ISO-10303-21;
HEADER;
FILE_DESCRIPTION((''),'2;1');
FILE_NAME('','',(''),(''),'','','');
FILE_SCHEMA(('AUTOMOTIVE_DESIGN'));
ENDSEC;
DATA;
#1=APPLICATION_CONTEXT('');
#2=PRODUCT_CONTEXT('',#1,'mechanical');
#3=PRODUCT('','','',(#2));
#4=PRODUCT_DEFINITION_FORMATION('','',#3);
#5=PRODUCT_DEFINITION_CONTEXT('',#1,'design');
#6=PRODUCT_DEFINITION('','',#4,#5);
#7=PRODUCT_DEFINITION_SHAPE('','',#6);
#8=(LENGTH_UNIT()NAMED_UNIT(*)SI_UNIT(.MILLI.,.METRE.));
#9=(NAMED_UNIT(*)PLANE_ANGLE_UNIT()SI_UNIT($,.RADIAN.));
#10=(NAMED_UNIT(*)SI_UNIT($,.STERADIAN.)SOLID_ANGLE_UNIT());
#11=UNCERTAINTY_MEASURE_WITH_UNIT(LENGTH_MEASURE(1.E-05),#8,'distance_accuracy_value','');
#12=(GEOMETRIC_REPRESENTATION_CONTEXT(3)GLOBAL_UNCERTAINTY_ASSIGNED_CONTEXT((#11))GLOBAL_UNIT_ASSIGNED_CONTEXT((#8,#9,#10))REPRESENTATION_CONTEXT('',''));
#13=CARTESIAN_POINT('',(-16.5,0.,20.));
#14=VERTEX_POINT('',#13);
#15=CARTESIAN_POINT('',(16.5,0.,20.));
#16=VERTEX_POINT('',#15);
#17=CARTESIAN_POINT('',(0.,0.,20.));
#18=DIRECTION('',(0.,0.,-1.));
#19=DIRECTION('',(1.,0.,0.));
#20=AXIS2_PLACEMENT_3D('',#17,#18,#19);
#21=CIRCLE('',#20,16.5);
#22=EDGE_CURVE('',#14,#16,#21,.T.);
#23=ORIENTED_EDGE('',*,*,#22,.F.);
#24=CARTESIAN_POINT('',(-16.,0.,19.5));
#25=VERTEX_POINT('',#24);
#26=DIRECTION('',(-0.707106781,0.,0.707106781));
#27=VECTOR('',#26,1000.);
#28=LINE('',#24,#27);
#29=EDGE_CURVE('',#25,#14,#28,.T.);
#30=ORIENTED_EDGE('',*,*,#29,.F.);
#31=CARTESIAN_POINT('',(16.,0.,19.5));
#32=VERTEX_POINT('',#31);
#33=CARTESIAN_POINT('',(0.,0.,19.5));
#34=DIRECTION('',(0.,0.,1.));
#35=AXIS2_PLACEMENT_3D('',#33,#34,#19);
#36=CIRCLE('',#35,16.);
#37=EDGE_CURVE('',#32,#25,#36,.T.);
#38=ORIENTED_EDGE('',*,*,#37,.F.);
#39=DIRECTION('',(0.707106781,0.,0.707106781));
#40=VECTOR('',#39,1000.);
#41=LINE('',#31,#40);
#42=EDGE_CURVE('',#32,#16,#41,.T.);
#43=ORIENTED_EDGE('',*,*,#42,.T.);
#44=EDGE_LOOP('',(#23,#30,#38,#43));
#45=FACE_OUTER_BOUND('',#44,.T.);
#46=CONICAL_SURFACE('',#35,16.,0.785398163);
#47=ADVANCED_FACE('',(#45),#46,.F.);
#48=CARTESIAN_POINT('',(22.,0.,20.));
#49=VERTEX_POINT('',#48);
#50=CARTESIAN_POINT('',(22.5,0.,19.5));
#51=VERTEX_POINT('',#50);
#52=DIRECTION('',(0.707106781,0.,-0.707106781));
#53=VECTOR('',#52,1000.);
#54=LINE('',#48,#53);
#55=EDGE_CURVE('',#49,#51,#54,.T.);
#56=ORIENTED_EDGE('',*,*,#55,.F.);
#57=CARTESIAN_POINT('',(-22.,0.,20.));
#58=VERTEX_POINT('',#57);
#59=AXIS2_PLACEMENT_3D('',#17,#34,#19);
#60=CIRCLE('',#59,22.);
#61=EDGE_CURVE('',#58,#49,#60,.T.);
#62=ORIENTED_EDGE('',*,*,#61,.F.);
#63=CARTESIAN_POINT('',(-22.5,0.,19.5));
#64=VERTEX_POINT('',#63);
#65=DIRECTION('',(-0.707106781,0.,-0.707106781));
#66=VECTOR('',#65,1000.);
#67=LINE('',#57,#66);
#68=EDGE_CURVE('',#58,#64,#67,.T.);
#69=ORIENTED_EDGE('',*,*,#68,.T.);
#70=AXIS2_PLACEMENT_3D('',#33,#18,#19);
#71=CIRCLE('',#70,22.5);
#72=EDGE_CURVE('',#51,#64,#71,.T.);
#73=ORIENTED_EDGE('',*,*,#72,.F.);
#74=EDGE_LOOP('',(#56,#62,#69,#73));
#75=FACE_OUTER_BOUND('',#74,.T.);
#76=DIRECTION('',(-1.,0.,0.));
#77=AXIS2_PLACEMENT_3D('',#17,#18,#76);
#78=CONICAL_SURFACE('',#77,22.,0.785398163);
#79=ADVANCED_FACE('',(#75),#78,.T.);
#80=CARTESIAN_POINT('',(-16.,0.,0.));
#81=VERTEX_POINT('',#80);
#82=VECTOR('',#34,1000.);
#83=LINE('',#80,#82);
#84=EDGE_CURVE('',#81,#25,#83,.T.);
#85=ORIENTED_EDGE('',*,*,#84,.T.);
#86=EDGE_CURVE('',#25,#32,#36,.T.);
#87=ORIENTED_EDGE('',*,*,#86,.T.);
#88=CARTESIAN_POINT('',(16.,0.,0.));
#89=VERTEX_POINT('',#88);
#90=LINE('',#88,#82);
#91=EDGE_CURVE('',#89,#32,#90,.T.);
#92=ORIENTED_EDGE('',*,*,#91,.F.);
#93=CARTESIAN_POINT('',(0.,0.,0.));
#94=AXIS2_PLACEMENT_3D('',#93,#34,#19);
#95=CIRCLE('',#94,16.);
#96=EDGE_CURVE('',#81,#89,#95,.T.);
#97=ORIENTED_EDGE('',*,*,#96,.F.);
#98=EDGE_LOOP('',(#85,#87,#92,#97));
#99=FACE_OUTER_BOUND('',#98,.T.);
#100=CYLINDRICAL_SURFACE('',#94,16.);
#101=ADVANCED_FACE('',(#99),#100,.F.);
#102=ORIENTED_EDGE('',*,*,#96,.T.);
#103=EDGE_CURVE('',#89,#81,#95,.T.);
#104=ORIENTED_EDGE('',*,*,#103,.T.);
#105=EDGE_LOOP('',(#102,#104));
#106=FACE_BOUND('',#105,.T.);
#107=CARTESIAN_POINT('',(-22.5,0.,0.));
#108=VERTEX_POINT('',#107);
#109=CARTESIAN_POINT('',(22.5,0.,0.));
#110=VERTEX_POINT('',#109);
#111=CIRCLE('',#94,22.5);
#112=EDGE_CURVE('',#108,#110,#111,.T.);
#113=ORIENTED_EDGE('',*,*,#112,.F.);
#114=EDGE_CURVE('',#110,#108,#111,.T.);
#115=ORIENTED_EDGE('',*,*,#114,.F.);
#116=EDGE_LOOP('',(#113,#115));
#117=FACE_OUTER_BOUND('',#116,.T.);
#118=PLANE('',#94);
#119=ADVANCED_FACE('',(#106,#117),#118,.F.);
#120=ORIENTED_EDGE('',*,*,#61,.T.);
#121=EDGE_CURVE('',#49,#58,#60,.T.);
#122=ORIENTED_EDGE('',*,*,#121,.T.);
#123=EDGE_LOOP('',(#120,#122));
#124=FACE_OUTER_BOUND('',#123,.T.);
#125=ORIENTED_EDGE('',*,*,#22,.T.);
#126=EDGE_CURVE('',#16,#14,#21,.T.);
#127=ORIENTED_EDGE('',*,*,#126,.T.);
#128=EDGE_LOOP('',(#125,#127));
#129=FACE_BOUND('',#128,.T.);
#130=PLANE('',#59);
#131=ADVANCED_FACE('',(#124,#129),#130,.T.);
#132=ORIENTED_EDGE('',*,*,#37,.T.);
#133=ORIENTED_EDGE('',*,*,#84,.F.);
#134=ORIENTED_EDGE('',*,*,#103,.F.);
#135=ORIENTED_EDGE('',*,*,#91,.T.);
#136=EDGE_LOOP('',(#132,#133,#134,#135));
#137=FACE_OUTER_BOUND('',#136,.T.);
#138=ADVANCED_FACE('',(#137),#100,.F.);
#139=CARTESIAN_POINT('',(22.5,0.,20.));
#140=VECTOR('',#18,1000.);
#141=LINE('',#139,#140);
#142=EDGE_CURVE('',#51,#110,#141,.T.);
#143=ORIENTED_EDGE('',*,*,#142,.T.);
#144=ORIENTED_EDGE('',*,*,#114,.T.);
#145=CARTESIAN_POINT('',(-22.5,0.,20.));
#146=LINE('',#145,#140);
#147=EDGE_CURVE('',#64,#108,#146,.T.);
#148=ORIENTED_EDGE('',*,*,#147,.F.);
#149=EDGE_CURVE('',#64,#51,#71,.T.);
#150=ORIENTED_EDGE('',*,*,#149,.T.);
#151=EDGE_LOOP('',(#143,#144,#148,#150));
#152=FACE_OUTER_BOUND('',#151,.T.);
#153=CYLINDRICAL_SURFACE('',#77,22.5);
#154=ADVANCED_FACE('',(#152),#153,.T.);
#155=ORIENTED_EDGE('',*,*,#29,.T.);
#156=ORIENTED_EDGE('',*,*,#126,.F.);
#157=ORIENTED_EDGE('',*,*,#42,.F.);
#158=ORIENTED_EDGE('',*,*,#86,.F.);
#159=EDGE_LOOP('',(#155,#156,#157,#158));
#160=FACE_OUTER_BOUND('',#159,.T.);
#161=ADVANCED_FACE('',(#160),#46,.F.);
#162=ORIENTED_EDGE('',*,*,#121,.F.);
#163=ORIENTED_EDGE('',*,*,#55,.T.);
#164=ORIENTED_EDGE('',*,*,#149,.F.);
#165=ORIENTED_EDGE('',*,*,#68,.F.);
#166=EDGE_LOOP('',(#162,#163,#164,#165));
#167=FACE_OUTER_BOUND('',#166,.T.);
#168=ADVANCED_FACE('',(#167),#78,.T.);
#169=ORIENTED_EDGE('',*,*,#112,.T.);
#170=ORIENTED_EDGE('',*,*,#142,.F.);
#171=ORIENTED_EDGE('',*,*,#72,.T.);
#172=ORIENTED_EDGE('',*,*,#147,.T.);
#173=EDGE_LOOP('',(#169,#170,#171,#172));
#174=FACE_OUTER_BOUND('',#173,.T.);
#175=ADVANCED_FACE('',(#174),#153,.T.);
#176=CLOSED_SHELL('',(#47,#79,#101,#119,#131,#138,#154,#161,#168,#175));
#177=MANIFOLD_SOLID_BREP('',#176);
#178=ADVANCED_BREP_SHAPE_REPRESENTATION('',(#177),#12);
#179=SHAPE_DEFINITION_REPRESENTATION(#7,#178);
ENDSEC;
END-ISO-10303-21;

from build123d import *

# Parameters (mm, degrees)
SKETCH_1_R          = 22.5
EXTRUDE_1_DEPTH     = 20
SKETCH_2_R          = 16
CUT_EXTRUDE_1_DEPTH = 20
CHAMFER_1_SIZE      = 0.5
CHAMFER_2_SIZE      = 0.5


with BuildPart() as part:
    # 草图1 → 凸台-拉伸1 (new body)
    with BuildSketch(Plane.XY):
        Circle(SKETCH_1_R)
    extrude(amount=EXTRUDE_1_DEPTH)

    # 草图2 → 切除-拉伸1 (cut)
    with BuildSketch(Plane.XY.offset(20)):
        Circle(SKETCH_2_R)
    extrude(amount=-CUT_EXTRUDE_1_DEPTH, mode=Mode.SUBTRACT)

    # 倒角1
    chamfer_1_edges = [part.edges().sort_by_distance(p)[0] for p in [
        (-16, 0, 20),
    ]]
    chamfer(chamfer_1_edges, length=CHAMFER_1_SIZE)

    # 倒角2
    chamfer_2_edges = [part.edges().sort_by_distance(p)[0] for p in [
        (-22.5, 0, 20),
    ]]
    chamfer(chamfer_2_edges, length=CHAMFER_2_SIZE)


solid = part.part
